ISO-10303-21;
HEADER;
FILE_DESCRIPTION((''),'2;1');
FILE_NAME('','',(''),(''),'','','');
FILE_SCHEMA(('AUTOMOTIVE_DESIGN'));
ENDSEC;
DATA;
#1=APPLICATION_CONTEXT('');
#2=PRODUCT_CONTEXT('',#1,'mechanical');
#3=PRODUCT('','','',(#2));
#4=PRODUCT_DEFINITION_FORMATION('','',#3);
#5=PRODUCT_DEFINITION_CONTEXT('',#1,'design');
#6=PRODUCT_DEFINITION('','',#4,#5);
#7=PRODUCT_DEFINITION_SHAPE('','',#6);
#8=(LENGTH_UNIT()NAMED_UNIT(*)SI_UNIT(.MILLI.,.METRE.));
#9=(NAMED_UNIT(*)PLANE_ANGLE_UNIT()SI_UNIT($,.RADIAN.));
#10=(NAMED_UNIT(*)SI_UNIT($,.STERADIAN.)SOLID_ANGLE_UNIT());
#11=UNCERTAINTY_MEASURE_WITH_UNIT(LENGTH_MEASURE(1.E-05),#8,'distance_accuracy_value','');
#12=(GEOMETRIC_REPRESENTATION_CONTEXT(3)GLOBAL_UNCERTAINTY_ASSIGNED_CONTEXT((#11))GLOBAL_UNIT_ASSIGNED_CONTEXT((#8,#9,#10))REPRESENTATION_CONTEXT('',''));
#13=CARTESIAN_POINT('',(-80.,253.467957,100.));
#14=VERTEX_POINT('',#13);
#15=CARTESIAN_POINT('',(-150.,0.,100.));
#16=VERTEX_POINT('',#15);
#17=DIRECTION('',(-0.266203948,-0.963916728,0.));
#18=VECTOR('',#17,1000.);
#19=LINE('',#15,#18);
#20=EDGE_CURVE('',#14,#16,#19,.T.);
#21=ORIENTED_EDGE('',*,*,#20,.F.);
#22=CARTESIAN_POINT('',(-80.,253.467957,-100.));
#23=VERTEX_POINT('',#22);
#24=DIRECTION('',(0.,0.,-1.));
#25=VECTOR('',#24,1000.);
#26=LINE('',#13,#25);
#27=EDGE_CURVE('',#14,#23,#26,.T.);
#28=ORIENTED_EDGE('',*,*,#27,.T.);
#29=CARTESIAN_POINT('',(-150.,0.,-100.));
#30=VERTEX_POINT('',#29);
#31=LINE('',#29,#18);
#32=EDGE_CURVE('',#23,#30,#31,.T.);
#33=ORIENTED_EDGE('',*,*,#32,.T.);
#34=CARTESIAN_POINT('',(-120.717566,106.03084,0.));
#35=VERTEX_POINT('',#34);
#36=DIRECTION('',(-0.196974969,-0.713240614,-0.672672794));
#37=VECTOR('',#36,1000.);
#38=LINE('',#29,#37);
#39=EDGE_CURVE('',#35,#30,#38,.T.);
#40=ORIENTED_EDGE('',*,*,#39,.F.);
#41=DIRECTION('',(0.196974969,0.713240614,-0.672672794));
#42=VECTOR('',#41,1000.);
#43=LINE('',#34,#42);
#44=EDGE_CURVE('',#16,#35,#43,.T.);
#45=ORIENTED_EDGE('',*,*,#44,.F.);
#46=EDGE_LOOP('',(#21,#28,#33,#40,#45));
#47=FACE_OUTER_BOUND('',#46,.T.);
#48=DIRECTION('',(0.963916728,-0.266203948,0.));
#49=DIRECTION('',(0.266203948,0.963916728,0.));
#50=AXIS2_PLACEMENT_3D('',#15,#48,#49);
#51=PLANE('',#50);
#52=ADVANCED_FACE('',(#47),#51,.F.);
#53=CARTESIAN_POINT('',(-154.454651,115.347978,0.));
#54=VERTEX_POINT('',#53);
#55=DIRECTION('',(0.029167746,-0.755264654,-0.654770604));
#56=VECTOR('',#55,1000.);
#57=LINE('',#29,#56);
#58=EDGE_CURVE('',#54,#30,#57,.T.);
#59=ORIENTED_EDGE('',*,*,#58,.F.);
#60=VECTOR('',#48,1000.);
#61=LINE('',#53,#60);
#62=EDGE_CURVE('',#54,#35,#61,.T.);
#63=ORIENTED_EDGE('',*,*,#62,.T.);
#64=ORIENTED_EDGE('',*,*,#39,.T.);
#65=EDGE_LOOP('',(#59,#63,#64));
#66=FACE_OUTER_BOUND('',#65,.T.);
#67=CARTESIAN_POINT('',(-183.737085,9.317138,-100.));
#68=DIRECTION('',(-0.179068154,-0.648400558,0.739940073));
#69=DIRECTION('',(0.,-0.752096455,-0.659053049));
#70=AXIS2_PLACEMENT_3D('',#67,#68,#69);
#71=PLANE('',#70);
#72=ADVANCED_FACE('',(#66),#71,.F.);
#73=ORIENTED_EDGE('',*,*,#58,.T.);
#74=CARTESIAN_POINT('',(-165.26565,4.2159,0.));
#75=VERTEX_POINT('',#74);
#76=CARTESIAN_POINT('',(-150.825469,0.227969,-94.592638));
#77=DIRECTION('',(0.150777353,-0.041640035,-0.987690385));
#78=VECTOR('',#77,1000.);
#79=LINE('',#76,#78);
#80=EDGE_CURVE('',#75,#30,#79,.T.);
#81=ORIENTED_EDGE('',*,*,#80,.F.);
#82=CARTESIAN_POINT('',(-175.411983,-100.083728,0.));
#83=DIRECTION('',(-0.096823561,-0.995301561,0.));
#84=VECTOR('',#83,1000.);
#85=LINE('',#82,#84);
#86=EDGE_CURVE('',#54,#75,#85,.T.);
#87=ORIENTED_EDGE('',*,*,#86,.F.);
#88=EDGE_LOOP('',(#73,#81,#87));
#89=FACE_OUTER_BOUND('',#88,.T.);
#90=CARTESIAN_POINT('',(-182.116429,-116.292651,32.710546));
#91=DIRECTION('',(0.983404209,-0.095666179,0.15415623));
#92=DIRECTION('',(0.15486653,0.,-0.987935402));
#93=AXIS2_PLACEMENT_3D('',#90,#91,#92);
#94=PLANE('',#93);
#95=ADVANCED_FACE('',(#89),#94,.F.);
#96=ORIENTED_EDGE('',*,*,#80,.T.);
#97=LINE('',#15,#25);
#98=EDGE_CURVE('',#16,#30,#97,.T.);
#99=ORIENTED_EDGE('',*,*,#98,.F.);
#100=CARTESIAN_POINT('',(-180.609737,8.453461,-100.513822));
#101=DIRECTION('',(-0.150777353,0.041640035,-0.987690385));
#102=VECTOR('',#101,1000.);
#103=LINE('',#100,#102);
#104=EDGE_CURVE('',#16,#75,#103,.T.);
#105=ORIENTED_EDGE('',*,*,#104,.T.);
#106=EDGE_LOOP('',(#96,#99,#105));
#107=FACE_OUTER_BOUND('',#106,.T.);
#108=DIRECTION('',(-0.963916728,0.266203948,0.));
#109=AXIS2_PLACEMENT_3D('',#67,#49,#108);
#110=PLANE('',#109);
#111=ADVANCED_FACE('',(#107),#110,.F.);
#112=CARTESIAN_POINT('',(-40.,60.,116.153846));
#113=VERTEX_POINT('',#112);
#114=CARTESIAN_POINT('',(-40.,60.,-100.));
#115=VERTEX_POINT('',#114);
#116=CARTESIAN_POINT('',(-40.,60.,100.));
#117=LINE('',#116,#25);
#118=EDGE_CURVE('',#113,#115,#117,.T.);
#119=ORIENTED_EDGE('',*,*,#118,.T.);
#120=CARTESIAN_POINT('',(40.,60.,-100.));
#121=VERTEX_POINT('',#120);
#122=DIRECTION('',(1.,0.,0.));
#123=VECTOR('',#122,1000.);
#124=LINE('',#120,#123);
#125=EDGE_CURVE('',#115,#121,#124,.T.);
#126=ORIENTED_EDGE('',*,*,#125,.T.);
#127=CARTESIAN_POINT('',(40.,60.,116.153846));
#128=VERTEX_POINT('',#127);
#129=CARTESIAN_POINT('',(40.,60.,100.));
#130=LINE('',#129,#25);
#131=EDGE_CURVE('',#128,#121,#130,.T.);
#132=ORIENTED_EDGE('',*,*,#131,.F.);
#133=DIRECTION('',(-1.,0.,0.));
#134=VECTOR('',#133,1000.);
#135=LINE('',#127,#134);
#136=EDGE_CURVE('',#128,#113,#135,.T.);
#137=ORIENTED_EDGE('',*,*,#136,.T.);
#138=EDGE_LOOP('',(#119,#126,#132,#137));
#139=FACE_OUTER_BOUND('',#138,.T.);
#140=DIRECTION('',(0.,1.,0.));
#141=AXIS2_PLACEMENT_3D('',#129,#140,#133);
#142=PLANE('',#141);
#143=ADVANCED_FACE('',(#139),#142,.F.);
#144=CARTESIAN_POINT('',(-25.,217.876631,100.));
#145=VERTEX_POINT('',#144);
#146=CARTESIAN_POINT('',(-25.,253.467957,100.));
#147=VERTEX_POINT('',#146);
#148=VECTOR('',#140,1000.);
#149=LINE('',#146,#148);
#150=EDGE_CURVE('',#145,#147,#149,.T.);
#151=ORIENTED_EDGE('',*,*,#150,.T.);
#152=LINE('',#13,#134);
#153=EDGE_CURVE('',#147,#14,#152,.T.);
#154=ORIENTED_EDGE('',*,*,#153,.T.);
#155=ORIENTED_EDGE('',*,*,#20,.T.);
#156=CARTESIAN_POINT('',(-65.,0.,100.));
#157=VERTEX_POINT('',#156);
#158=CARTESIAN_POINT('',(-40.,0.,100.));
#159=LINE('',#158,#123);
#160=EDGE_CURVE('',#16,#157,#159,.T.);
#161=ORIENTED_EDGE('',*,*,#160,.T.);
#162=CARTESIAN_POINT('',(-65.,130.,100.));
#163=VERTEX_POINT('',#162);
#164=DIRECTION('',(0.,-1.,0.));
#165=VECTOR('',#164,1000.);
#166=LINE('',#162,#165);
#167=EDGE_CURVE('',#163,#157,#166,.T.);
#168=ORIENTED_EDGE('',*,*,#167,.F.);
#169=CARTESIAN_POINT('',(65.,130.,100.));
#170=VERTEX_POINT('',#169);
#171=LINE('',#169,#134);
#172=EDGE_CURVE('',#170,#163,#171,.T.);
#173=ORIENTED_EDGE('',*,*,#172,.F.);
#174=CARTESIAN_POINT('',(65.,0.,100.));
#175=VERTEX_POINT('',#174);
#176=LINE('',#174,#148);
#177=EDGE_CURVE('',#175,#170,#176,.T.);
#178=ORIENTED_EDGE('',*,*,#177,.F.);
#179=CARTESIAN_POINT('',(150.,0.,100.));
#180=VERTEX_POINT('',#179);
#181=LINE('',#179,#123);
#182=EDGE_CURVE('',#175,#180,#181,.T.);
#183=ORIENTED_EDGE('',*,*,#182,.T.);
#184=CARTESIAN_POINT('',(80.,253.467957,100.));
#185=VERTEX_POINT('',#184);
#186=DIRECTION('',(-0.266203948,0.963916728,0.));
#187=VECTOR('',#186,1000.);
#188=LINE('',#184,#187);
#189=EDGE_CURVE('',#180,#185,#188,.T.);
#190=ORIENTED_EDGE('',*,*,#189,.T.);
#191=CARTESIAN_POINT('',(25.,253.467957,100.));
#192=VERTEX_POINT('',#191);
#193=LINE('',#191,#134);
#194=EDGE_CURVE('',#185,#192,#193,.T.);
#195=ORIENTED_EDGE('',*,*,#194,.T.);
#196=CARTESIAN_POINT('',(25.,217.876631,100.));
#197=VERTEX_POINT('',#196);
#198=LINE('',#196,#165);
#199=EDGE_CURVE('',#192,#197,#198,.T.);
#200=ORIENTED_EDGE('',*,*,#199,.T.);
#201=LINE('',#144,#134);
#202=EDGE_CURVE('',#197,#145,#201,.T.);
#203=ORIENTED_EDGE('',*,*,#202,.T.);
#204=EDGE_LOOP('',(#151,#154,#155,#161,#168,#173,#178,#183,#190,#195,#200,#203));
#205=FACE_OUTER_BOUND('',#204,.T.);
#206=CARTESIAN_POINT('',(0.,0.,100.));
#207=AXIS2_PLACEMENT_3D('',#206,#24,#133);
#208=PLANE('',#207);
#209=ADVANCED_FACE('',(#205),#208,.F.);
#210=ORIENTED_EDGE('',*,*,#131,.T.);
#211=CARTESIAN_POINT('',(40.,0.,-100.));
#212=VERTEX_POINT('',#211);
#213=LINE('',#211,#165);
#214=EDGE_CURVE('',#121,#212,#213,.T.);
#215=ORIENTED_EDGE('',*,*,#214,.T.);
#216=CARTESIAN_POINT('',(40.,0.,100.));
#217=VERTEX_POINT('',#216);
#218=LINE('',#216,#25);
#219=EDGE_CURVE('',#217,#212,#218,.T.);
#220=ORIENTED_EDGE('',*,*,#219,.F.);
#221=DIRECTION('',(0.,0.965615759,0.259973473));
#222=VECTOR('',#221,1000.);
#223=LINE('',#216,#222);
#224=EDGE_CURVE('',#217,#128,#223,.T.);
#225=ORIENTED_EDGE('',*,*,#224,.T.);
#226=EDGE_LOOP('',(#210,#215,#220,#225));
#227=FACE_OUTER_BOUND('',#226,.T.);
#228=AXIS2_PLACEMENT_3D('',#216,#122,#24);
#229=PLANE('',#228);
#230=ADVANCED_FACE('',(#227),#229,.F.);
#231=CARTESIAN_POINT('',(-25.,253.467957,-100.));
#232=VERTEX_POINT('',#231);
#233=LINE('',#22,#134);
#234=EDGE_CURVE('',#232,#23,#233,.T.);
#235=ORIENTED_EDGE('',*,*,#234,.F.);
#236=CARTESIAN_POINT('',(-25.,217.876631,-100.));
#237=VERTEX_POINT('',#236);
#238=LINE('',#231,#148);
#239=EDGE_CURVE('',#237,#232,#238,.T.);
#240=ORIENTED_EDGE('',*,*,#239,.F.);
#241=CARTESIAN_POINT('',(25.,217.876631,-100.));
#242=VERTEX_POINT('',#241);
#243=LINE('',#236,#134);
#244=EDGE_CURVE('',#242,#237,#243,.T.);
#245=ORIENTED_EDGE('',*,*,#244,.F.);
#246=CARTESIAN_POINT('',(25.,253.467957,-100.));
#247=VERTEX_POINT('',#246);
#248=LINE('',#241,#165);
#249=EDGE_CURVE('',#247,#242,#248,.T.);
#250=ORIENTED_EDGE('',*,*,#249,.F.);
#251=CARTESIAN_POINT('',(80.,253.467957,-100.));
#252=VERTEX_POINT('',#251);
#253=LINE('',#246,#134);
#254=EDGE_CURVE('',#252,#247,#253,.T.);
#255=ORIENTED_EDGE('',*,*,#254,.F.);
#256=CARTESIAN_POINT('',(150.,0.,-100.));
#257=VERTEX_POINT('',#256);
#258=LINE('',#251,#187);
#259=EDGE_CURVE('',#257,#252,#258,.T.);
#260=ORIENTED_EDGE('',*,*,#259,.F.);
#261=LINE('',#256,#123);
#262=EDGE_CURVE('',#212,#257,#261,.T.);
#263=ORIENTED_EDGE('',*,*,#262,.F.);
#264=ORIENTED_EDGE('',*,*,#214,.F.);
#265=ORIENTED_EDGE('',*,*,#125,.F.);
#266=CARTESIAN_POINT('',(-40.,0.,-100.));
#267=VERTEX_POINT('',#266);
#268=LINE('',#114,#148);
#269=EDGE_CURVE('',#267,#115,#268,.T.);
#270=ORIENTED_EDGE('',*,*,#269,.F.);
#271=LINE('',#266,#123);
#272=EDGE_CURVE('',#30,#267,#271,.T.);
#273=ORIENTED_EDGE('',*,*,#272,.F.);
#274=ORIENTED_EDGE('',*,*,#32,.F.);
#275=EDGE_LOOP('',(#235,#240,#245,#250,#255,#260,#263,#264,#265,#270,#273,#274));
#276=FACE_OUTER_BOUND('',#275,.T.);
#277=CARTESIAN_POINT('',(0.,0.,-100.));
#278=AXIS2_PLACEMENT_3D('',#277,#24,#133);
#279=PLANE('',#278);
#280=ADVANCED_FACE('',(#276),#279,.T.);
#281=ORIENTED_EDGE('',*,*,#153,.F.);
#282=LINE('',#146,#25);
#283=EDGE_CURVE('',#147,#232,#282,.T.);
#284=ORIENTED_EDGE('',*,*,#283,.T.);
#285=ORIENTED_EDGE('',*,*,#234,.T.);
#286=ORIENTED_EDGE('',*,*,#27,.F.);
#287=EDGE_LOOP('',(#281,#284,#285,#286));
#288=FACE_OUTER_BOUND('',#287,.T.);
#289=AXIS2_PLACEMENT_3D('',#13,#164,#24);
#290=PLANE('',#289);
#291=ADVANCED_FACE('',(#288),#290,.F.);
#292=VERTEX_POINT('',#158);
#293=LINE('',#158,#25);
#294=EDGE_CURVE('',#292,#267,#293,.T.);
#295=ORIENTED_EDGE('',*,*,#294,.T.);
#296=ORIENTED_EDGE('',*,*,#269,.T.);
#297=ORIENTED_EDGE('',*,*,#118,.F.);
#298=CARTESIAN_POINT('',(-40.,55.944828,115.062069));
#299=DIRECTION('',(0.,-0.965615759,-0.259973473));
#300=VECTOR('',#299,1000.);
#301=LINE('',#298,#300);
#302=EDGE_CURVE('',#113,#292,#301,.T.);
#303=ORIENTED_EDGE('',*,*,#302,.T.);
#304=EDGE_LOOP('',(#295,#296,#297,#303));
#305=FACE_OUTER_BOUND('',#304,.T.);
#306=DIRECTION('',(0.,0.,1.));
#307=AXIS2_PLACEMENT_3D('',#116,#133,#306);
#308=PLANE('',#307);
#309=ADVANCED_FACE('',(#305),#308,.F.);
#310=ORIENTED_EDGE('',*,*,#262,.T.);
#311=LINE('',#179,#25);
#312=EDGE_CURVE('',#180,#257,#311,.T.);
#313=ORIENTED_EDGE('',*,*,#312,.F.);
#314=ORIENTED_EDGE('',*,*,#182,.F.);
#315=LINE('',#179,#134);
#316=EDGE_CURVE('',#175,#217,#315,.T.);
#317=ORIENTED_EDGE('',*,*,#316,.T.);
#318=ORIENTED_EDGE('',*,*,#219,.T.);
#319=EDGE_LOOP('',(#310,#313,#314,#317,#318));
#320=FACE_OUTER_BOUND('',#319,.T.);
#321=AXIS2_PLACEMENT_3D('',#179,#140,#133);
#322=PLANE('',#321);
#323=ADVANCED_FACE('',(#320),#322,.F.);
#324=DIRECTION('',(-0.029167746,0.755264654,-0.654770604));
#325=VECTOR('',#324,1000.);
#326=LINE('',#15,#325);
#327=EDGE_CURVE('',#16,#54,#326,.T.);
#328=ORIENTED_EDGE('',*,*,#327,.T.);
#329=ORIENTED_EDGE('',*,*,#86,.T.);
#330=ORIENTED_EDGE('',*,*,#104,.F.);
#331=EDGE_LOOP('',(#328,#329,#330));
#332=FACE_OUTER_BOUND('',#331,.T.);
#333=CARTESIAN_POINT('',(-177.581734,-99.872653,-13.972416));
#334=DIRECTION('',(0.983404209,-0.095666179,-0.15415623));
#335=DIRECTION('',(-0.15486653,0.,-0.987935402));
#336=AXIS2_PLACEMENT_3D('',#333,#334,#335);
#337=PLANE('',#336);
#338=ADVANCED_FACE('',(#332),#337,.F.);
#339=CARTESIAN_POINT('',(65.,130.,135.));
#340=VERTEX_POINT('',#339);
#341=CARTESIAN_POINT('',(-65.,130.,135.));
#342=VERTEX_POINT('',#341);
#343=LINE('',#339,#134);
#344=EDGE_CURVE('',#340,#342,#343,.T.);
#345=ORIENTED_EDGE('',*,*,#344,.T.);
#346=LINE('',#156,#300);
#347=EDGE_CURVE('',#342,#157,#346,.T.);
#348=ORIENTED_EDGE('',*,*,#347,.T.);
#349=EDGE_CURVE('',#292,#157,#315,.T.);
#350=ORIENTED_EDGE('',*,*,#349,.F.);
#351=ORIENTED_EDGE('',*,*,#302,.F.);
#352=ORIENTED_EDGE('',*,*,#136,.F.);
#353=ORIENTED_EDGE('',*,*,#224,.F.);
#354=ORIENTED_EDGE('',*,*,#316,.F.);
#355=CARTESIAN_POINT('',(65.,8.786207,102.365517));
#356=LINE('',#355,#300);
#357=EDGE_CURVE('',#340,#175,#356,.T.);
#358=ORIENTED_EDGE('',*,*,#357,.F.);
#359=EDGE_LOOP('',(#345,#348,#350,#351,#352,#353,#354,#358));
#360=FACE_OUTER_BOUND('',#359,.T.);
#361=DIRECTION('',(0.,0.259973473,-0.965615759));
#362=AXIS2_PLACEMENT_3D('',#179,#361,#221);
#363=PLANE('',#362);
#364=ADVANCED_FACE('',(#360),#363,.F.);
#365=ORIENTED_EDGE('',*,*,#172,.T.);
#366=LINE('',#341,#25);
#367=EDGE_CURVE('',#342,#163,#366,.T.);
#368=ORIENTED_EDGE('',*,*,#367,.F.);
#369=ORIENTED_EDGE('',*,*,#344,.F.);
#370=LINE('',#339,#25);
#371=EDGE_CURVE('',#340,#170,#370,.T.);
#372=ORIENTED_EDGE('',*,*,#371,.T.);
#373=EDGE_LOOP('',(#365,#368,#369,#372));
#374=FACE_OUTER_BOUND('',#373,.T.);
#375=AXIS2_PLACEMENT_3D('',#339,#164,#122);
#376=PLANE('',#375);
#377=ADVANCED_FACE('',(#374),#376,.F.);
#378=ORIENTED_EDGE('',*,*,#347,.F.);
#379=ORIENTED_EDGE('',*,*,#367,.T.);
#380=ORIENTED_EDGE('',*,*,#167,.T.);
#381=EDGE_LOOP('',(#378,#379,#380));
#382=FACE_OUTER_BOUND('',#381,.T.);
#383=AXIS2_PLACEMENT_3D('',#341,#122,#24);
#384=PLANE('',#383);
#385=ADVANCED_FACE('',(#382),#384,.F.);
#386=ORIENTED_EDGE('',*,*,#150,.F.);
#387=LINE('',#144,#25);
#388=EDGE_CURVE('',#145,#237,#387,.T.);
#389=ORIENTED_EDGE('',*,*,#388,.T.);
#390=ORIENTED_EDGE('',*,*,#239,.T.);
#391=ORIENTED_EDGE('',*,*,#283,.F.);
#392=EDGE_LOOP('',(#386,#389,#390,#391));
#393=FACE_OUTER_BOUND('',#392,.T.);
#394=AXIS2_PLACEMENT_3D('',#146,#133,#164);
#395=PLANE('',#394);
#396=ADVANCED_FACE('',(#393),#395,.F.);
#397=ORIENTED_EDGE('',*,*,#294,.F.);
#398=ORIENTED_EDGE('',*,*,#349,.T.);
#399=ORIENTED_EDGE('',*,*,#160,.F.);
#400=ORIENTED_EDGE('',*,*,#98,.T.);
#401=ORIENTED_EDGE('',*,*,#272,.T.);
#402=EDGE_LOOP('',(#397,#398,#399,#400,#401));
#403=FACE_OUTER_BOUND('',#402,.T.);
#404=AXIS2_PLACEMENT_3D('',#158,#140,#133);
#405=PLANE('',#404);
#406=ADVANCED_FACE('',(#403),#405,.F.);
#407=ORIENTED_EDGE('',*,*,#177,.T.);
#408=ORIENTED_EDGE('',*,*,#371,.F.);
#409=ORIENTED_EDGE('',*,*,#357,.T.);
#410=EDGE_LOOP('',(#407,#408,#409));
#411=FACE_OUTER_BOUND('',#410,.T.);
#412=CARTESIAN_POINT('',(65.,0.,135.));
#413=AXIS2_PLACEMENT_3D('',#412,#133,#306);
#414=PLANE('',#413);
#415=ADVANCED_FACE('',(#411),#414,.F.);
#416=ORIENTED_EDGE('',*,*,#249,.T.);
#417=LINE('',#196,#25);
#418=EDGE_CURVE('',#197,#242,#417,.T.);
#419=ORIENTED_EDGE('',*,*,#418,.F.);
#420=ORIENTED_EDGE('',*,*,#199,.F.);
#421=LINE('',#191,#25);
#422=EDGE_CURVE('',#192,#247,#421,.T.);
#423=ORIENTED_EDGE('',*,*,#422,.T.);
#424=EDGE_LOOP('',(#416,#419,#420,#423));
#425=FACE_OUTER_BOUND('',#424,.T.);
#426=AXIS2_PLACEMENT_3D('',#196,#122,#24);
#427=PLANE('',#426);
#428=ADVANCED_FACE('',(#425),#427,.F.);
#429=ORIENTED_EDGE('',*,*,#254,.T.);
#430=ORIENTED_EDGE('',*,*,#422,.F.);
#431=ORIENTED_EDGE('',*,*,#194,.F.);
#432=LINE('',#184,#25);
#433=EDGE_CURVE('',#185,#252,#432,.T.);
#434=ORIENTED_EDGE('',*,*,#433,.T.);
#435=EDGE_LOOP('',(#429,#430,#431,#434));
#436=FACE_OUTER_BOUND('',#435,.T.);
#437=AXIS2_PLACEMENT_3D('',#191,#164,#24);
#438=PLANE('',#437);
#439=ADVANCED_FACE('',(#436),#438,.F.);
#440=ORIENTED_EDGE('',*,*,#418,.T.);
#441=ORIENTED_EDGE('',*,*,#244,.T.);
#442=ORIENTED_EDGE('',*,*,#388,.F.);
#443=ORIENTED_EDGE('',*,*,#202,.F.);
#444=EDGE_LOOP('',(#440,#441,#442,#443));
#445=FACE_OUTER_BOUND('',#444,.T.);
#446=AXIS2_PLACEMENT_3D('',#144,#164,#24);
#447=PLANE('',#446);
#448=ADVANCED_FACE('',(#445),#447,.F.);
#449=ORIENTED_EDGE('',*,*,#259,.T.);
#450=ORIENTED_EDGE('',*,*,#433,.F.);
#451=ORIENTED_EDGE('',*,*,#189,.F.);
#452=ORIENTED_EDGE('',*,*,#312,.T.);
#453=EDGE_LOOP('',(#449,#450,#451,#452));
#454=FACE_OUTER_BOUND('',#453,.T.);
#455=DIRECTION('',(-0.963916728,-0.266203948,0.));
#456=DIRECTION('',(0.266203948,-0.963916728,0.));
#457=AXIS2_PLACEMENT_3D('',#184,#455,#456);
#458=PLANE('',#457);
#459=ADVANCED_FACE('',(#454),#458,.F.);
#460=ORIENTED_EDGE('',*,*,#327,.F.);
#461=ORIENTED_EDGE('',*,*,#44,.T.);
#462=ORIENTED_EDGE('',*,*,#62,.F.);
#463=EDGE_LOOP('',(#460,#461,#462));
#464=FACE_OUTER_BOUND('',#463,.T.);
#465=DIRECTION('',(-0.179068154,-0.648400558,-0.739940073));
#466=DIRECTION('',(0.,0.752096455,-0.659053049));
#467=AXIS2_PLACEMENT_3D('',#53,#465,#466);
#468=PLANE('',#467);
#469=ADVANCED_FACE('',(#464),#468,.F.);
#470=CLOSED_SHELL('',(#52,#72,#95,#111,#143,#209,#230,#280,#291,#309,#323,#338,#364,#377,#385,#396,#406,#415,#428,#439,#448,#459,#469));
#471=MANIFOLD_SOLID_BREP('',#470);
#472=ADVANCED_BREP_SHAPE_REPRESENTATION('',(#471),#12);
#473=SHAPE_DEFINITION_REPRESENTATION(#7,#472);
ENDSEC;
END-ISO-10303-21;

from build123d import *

# Parameters (mm, degrees)
PEDESTAL_BODY_DEPTH  = 100
FRONT_BOSS_DEPTH     = 35
FRONT_BOSS_CUT_DEPTH = 359.742254771
TOP_BOSS_DEPTH       = 35
TOP_BOSS_CUT_A_DEPTH = 324.745166661
TOP_BOSS_CUT_B_DEPTH = 339.016839686


with BuildPart() as part:
    # Pedestal Profile Sketch → Pedestal Body (new, symmetric)
    with BuildSketch(Plane.XY):
        Polygon((40, 0), (40, 60), (-40, 60), (-40, 0), (-150, 0), (-80, 253.467957262), (-25, 253.467957262), (-25, 217.876631195), (25, 217.876631195), (25, 253.467957262), (80, 253.467957262), (150, 0), align=None)
    extrude(amount=PEDESTAL_BODY_DEPTH, both=True)

    # Front Boss Sketch → Front Boss (add)
    with BuildSketch(Plane.XY.offset(100)):
        Polygon((40, 0), (65, 0), (65, 130), (-65, 130), (-65, 0), (-40, 0), (-40, 60), (40, 60), align=None)
    extrude(amount=FRONT_BOSS_DEPTH)

    # Front Boss Cut Sketch → Front Boss Cut (cut, through all)
    with BuildSketch(Plane.ZY.offset(65)):
        Polygon((100, 0), (135, 130), (135, 0), align=None)
    extrude(amount=-FRONT_BOSS_CUT_DEPTH, mode=Mode.SUBTRACT)

    # Top Boss Sketch → Top Boss (add)
    with BuildSketch(Plane(origin=(-139.370318702, 38.489765785, 0), x_dir=(0, 0, 1), z_dir=(-0.9639167277376053, 0.26620394810676146, 0))):
        Polygon((-100, -39.930592216), (0, 70.069407784), (100, -39.930592216), align=None)
    extrude(amount=TOP_BOSS_DEPTH)

    # Top Boss Cut A Sketch → Top Boss Cut A (cut, through all)
    with BuildSketch(Plane(origin=(8.440159726, 30.561572066, 34.87617582), x_dir=(0.9838366716003674, -0.11801541262610508, -0.13467652355552237), z_dir=(0.1790681535458246, 0.6484005584270376, 0.7399400733959439))):
        Polygon((-161.043153096, -65.90530493), (-165.570989176, 86.752805567), (-195.334500882, -58.897918327), align=None)
    extrude(amount=-TOP_BOSS_CUT_A_DEPTH, mode=Mode.SUBTRACT)

    # Top Boss Cut B Sketch → Top Boss Cut B (cut, through all)
    with BuildSketch(Plane(origin=(8.440159726, 30.561572066, -34.87617582), x_dir=(-0.9838366716003674, 0.11801541262610508, -0.13467652355552237), z_dir=(0.1790681535458246, 0.6484005584270376, -0.7399400733959439))):
        Polygon((161.043153096, -65.90530493), (165.570989176, 86.752805567), (192.07604702, -59.563778593), align=None)
    extrude(amount=-TOP_BOSS_CUT_B_DEPTH, mode=Mode.SUBTRACT)


solid = part.part
